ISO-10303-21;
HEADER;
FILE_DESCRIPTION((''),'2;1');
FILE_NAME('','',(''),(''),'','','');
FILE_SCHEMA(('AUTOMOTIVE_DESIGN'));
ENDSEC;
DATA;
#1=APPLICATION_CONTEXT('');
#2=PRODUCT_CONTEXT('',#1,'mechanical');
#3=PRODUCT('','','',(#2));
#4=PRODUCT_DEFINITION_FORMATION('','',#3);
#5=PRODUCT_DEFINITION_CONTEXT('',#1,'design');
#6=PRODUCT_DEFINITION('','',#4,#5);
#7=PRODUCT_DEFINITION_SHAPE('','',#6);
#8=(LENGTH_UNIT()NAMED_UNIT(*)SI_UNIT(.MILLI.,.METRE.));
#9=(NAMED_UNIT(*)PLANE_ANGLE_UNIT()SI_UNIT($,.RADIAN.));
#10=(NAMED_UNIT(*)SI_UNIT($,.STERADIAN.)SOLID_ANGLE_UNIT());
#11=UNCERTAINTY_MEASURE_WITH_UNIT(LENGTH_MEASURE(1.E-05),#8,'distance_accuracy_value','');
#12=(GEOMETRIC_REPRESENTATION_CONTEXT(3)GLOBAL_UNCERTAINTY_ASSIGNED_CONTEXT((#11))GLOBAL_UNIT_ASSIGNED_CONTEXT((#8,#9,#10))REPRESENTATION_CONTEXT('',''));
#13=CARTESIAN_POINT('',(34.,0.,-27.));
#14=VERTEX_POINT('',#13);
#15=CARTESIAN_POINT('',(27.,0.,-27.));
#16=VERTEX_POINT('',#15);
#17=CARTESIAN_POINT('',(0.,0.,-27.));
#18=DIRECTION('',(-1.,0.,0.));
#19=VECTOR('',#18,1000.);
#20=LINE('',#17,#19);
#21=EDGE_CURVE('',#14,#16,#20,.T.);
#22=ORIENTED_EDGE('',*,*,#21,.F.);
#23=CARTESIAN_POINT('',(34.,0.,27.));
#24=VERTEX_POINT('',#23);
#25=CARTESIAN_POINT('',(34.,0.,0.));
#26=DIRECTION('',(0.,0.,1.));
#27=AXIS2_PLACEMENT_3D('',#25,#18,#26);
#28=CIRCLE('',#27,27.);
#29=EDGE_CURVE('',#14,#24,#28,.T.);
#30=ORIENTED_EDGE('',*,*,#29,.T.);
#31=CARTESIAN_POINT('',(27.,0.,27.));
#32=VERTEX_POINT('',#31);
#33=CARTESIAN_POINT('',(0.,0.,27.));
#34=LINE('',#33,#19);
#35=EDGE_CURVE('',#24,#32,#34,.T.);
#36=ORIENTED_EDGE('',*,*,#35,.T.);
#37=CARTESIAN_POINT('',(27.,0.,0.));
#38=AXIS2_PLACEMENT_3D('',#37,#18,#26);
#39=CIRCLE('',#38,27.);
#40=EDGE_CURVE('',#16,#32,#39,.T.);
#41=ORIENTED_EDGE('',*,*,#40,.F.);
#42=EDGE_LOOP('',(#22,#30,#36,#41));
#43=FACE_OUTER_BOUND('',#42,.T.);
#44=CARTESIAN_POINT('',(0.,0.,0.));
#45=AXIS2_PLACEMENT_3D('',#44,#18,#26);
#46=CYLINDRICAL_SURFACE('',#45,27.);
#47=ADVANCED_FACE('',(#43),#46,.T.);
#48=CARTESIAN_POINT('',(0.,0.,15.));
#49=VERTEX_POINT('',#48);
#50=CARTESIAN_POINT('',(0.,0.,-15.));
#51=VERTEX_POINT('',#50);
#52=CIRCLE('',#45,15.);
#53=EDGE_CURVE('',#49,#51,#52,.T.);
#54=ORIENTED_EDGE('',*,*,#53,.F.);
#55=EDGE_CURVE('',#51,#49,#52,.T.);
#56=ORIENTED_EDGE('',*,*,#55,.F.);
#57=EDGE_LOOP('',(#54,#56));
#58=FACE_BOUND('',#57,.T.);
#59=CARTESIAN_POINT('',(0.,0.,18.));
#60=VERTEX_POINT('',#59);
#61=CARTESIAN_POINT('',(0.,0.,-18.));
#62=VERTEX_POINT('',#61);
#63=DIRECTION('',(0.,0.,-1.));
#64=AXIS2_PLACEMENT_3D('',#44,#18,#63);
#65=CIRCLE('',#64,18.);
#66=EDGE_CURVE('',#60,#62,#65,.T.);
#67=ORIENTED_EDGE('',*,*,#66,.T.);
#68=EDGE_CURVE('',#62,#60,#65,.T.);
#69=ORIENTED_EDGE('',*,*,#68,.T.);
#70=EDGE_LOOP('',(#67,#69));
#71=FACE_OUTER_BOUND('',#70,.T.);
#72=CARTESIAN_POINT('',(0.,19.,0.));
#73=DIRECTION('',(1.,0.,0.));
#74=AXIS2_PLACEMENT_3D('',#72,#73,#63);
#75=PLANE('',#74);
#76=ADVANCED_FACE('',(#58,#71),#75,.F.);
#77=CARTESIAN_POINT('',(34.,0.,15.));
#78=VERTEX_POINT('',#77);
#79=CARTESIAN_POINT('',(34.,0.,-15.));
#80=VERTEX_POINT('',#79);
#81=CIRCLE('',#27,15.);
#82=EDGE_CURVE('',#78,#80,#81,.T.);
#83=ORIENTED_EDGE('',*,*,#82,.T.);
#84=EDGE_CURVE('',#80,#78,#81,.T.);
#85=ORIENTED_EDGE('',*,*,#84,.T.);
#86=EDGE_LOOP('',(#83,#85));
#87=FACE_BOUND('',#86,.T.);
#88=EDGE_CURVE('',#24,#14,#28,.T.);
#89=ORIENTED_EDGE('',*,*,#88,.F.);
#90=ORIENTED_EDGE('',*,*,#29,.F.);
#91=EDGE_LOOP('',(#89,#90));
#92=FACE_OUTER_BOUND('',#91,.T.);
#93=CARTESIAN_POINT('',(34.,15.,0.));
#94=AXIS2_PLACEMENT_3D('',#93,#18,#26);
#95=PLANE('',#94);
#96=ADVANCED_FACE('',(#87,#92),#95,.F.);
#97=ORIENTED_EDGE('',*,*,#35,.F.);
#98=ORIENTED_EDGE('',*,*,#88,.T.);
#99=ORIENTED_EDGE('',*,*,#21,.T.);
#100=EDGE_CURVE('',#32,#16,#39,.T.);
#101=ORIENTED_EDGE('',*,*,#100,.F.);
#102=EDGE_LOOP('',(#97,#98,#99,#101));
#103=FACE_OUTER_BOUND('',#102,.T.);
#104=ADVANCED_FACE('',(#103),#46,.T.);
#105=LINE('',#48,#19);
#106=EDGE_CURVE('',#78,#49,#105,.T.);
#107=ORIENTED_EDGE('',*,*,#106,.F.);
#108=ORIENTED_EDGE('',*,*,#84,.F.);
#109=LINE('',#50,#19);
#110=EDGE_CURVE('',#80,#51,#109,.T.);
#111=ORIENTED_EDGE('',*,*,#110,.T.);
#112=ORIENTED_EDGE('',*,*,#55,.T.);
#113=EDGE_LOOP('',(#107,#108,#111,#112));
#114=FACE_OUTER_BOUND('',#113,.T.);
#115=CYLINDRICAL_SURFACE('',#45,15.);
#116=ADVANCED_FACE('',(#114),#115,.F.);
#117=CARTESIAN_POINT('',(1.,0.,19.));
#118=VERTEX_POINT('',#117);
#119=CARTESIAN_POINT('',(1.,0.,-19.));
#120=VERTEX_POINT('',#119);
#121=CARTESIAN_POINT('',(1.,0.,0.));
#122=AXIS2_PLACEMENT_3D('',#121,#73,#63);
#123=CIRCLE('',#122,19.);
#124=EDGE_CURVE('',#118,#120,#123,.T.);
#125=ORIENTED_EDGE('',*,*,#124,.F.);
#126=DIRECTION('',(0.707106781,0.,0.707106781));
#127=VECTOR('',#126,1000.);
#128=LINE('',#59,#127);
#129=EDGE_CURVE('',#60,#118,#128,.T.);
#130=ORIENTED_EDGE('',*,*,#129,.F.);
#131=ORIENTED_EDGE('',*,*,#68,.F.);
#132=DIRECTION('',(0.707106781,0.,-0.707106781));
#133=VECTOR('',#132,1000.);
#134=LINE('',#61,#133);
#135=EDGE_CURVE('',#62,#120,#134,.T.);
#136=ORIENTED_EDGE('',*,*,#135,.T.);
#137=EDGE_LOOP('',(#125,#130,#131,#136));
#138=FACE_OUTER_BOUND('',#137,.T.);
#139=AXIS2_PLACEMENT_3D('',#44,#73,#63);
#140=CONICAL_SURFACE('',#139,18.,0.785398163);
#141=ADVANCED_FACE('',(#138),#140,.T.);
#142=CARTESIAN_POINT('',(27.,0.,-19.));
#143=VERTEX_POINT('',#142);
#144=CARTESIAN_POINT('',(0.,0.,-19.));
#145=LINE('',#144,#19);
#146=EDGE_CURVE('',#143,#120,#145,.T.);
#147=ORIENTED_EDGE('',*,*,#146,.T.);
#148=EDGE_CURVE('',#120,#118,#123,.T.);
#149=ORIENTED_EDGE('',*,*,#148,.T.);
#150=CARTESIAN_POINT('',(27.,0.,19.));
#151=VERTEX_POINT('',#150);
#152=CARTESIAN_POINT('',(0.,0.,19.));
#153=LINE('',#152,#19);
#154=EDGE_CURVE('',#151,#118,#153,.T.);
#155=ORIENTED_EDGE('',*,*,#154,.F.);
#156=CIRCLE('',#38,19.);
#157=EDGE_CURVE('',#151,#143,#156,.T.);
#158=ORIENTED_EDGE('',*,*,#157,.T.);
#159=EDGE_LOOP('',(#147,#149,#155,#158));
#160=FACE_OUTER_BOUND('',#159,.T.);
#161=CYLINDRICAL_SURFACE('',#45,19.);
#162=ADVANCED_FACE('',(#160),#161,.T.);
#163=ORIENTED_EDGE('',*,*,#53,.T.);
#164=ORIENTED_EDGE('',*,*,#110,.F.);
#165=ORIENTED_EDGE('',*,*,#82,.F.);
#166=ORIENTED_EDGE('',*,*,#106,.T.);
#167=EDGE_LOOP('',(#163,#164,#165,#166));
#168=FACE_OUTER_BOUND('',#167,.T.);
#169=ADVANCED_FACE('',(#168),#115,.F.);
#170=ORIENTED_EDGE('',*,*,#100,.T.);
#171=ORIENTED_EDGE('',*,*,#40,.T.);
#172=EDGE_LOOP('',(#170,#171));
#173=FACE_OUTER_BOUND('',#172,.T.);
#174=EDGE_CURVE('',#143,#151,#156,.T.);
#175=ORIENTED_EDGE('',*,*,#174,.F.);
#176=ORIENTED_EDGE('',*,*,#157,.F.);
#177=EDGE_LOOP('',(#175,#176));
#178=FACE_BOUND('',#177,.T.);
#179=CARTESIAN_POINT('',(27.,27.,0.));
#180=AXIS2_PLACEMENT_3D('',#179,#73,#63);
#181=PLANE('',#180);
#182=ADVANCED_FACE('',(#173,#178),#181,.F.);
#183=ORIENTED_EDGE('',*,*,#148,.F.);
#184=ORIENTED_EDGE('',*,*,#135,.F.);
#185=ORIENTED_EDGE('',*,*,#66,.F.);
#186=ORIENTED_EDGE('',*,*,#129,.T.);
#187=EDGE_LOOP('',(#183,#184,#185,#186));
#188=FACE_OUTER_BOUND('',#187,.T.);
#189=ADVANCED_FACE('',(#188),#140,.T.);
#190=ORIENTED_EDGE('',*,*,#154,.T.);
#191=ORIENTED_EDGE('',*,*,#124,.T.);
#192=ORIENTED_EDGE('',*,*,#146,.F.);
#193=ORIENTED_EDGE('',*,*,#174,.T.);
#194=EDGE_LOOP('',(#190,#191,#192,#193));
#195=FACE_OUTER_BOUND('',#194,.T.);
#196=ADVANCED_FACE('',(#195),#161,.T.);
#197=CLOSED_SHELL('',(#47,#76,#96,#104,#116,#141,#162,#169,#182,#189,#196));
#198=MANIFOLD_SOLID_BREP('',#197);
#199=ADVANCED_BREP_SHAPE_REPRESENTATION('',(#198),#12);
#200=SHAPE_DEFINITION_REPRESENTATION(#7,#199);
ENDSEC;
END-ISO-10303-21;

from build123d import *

# Parameters (mm, degrees)
CHAMFER1_SIZE = 1


with BuildPart() as part:
    # Sketch1 → Revolve1 (revolve)
    with BuildSketch(Plane.XY, mode=Mode.PRIVATE) as revolve1_sk:
        Polygon((0, 15), (34, 15), (34, 27), (27, 27), (27, 19), (0, 19), align=None)
    revolve(revolve1_sk.sketch.rotate(Axis((0, 0, 0), (1, 0, 0)), 90), axis=Axis((0, 0, 0), (1, 0, 0)))

    # Chamfer1
    chamfer1_edges = [part.edges().sort_by_distance(p)[0] for p in [
        (0, 0, -19),
    ]]
    chamfer(chamfer1_edges, length=CHAMFER1_SIZE)


solid = part.part
